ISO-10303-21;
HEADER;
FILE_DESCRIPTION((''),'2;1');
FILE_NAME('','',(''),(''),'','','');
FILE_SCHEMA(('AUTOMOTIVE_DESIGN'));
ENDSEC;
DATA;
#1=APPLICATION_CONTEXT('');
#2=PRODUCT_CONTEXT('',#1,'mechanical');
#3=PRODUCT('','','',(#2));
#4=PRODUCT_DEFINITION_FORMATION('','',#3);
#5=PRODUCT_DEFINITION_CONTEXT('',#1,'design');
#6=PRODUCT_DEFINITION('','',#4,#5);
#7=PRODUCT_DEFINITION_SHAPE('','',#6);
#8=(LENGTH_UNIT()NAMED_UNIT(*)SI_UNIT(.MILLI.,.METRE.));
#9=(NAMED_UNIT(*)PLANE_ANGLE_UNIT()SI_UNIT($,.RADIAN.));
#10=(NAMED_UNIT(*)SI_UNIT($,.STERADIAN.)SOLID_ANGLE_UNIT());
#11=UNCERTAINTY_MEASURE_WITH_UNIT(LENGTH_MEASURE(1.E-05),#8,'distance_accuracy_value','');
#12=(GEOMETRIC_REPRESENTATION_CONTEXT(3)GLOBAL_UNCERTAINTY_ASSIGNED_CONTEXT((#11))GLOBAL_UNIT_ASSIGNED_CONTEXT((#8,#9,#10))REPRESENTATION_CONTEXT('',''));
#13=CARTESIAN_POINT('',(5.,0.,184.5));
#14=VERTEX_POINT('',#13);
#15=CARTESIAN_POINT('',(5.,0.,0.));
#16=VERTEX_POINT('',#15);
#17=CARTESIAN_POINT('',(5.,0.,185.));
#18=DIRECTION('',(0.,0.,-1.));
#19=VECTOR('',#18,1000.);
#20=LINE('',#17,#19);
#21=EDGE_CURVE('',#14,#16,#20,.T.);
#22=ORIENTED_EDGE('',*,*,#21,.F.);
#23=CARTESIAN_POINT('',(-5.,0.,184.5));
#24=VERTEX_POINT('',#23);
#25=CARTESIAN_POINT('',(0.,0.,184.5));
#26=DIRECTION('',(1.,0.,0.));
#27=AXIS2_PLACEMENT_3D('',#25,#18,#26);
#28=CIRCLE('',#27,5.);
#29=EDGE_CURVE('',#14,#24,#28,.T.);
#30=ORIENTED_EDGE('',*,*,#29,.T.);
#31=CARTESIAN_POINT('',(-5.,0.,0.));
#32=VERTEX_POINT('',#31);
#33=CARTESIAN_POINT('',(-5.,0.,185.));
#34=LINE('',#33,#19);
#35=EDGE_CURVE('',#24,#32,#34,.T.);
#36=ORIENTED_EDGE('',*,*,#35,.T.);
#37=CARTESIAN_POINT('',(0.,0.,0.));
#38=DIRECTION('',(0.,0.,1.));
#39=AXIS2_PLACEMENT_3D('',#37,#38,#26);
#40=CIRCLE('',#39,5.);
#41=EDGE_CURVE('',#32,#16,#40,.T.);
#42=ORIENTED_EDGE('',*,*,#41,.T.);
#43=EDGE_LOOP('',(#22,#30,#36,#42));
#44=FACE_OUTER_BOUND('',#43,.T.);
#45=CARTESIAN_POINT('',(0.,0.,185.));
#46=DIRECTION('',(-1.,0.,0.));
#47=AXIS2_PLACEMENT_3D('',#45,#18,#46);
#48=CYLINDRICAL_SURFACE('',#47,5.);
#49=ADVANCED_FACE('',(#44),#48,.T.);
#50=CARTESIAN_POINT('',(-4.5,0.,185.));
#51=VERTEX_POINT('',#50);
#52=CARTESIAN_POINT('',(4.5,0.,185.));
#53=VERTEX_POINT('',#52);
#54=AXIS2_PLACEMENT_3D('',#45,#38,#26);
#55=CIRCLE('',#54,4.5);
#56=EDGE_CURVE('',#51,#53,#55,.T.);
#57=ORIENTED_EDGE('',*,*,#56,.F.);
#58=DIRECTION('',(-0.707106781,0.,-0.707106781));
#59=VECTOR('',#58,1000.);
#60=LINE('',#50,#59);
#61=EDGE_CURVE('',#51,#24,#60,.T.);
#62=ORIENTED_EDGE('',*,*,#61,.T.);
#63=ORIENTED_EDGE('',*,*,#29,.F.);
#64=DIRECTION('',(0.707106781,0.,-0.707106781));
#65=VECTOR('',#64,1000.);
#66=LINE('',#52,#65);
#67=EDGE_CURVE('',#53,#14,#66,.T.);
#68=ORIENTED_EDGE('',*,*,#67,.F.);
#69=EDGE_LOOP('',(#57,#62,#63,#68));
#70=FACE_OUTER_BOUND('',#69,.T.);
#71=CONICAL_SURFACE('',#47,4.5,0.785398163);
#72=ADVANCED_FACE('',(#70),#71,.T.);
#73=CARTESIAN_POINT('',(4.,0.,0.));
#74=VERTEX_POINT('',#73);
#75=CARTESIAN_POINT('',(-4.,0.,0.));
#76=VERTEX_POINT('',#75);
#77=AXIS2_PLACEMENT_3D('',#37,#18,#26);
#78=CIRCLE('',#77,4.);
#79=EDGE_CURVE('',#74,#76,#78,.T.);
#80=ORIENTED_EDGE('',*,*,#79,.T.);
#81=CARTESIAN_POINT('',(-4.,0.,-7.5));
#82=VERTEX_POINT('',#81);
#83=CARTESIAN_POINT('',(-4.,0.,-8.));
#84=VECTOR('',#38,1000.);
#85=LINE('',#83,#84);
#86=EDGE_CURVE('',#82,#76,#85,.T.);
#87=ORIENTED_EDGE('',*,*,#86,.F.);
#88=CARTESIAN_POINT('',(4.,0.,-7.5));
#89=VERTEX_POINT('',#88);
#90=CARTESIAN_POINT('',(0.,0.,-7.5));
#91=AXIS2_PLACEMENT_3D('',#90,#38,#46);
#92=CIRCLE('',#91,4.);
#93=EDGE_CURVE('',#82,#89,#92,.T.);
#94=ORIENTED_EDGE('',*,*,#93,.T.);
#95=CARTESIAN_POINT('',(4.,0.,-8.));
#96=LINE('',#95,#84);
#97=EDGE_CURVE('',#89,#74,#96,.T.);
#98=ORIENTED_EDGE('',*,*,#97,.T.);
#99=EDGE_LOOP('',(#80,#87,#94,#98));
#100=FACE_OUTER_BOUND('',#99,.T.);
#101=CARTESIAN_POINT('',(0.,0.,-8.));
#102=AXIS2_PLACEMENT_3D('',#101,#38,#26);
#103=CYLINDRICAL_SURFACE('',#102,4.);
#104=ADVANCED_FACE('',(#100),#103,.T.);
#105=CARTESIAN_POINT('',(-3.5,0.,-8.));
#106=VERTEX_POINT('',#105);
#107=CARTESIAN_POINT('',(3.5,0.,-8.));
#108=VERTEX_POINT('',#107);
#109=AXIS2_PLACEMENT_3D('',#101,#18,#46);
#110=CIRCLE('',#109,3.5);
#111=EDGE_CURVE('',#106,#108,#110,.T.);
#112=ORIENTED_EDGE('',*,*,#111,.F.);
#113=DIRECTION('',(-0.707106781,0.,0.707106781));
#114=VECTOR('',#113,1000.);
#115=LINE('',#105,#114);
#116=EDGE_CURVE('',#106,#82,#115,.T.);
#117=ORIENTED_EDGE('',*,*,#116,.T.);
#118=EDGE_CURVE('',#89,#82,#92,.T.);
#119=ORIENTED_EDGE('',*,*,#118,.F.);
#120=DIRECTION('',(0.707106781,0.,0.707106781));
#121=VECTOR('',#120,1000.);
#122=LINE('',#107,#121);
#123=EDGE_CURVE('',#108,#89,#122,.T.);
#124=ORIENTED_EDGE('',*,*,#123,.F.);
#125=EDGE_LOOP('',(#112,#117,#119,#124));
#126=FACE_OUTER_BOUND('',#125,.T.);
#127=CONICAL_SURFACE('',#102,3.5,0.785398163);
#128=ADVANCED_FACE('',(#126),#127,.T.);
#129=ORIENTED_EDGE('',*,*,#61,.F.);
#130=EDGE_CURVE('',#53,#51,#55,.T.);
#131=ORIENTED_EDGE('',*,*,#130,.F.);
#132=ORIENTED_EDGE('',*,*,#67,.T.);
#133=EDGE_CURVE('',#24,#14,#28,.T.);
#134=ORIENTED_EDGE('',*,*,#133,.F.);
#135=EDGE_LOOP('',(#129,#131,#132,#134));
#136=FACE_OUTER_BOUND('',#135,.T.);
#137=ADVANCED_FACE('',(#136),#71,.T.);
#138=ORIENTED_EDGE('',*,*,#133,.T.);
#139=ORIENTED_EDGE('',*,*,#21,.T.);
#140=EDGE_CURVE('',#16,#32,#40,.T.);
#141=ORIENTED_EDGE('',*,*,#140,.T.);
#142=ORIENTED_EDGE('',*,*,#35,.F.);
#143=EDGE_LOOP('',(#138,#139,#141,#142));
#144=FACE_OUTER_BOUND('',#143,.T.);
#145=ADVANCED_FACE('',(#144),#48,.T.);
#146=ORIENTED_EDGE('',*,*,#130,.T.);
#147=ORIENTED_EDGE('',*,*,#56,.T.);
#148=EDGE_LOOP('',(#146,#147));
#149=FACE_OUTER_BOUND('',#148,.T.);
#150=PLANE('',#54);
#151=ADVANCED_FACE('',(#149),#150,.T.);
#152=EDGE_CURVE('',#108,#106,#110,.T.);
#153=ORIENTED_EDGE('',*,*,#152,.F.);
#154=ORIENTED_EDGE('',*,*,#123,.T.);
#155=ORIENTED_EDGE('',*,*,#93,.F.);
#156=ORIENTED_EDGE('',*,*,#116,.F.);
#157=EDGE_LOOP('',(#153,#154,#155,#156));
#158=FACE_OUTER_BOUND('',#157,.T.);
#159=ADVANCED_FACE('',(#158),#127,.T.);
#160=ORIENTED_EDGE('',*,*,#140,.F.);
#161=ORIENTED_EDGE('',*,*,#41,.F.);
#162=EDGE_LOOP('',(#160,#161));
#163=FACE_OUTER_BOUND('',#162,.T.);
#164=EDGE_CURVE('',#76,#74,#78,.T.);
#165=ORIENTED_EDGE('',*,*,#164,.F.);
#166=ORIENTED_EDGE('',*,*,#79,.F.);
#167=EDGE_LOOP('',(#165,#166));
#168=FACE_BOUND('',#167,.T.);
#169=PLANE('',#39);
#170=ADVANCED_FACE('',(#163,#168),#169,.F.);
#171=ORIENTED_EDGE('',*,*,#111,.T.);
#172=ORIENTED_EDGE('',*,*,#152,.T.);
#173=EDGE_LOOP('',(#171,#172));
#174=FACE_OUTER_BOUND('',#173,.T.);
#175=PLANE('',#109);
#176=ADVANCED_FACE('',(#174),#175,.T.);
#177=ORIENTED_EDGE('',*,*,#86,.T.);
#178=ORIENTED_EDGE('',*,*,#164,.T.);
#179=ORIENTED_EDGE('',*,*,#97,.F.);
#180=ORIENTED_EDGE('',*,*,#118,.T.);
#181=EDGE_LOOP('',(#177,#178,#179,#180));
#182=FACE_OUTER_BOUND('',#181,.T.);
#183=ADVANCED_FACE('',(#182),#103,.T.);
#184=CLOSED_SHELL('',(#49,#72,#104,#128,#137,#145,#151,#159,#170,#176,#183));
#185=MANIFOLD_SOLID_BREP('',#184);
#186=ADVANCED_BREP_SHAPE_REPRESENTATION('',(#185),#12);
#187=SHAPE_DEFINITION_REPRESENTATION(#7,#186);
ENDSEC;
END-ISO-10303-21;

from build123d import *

# Parameters (mm, degrees)
SKETCH_1_R      = 5
EXTRUDE_1_DEPTH = 185
SKETCH_2_R      = 4
EXTRUDE_2_DEPTH = 8
CHAMFER_1_SIZE  = 0.5


with BuildPart() as part:
    # 草图1 → 凸台-拉伸1 (new body)
    with BuildSketch(Plane.XY):
        Circle(SKETCH_1_R)
    extrude(amount=EXTRUDE_1_DEPTH)

    # 草图2 → 凸台-拉伸2 (add)
    with BuildSketch(Plane(origin=(0, 0, 0), x_dir=(-1, 0, 0), z_dir=(0, 0, -1))):
        with Locations(Location((0, 0, 0), (0, 0, 180))):
            Circle(SKETCH_2_R)
    extrude(amount=EXTRUDE_2_DEPTH)

    # 倒角1
    chamfer_1_edges = [part.edges().sort_by_distance(p)[0] for p in [
        (-5, 0, 185),
        (-4, 0, -8),
    ]]
    chamfer(chamfer_1_edges, length=CHAMFER_1_SIZE)


solid = part.part
